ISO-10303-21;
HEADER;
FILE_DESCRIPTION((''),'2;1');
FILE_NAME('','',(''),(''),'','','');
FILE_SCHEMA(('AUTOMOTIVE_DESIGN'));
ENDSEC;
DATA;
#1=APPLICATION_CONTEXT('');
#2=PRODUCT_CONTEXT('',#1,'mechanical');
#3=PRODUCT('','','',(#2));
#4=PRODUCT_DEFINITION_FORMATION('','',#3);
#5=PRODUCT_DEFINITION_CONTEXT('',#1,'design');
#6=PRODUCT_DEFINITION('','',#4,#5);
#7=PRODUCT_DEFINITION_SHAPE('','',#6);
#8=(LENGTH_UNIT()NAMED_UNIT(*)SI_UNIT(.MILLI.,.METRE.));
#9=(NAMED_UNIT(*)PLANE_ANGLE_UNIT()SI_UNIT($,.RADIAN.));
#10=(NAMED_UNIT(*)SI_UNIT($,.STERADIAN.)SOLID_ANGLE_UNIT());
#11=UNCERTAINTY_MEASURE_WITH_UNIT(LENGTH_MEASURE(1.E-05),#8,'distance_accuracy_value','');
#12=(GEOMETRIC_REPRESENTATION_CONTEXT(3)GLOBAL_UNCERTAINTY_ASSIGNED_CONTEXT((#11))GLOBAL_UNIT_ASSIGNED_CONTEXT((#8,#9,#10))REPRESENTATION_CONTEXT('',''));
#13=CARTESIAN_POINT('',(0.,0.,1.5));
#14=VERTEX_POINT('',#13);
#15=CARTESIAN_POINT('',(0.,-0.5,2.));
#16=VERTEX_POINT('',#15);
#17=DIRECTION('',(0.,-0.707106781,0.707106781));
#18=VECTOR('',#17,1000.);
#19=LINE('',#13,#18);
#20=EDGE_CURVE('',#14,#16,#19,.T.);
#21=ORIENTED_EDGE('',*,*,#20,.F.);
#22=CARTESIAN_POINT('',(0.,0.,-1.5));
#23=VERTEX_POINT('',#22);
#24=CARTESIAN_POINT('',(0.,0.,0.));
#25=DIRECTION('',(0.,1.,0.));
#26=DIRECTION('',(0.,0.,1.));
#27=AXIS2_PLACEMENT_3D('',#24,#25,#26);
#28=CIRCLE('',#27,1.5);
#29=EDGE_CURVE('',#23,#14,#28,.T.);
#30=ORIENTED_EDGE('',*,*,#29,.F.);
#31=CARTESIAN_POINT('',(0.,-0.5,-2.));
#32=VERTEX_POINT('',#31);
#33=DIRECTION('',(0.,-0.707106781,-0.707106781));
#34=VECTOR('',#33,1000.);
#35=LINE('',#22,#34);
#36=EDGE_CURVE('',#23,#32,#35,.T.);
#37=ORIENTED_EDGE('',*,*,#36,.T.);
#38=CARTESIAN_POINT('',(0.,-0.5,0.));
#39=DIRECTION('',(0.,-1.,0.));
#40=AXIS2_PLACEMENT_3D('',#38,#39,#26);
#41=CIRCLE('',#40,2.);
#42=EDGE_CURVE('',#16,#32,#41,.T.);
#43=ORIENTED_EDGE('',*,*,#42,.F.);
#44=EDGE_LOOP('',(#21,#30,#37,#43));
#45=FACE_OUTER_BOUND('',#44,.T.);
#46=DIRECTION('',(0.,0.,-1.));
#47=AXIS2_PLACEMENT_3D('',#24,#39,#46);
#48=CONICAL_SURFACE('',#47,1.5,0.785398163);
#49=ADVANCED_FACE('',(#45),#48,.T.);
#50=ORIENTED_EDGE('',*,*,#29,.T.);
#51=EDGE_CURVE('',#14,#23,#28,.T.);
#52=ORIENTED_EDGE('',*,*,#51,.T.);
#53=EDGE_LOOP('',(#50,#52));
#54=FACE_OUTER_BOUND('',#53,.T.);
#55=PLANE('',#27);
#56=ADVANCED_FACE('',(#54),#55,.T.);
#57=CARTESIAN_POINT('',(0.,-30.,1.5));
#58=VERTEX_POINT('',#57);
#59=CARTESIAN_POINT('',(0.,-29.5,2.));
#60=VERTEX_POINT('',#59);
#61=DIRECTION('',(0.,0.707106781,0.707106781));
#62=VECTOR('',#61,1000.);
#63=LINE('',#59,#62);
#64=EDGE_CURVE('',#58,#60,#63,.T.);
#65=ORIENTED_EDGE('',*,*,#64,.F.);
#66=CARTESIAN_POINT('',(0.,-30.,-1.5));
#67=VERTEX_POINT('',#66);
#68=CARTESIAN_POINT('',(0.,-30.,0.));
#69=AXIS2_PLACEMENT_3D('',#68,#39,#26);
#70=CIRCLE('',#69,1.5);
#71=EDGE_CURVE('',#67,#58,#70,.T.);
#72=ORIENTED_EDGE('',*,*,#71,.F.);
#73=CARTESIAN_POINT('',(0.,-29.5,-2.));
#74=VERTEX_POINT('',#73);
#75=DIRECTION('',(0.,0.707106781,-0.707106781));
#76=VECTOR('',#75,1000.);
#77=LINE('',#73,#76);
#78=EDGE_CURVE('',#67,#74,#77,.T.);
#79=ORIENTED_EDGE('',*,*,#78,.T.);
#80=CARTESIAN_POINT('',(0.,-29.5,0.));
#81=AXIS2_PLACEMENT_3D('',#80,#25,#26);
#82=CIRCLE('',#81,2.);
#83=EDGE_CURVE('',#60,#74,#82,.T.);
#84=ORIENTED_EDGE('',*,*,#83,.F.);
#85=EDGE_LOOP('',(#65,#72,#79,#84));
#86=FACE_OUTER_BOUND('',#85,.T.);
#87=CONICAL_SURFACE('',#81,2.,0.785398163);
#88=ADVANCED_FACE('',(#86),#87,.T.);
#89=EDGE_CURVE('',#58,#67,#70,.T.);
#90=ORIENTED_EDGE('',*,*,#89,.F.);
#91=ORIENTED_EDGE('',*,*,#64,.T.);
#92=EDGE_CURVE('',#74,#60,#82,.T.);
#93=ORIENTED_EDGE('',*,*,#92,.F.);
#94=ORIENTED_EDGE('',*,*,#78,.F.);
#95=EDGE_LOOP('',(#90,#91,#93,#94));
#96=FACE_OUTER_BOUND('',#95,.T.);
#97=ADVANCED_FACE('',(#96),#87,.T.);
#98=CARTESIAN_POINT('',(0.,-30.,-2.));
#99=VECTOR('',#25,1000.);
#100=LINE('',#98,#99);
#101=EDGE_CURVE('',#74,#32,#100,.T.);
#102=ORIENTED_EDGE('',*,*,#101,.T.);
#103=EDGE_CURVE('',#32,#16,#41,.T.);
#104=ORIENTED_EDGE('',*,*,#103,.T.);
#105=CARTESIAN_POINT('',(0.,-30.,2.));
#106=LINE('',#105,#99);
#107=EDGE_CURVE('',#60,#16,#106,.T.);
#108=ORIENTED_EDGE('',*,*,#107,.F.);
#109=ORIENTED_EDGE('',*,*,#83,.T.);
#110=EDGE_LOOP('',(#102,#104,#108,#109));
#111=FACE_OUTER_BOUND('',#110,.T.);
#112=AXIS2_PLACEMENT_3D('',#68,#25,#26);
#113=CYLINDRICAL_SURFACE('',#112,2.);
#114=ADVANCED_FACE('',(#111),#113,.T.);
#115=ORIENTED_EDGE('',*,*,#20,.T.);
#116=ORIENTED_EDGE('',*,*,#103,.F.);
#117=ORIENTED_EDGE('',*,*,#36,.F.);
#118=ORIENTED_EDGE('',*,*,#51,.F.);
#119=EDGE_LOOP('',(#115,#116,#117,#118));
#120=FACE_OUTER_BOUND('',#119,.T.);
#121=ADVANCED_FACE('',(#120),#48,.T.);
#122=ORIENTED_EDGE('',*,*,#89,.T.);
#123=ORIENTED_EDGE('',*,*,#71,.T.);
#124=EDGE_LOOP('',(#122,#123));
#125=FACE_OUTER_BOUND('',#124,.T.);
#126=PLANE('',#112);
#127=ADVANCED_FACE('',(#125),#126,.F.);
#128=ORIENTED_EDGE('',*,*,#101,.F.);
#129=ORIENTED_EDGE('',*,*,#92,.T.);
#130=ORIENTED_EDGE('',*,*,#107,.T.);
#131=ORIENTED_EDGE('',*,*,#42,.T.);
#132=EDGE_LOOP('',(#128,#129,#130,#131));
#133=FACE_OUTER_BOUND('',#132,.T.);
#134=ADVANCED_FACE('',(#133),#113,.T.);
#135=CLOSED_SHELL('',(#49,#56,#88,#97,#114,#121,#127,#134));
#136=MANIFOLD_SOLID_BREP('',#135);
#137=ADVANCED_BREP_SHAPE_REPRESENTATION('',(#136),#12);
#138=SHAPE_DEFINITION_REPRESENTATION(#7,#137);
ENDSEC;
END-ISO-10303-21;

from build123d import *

# Parameters (mm, degrees)
SKETCH1_R           = 2
BOSS_EXTRUDE1_DEPTH = 30
CHAMFER1_SIZE       = 0.5


with BuildPart() as part:
    # Sketch1 → Boss-Extrude1 (new body)
    with BuildSketch(Plane(origin=(0, 0, 0), x_dir=(1, 0, 0), z_dir=(0, 1, 0))):
        with Locations(Location((0, 0, 0), (0, 0, 270))):
            Circle(SKETCH1_R)
    extrude(amount=-BOSS_EXTRUDE1_DEPTH)

    # Chamfer1
    chamfer1_edges = [part.edges().sort_by_distance(p)[0] for p in [
        (0, 0, -2),
        (0, -30, -2),
    ]]
    chamfer(chamfer1_edges, length=CHAMFER1_SIZE)


solid = part.part
